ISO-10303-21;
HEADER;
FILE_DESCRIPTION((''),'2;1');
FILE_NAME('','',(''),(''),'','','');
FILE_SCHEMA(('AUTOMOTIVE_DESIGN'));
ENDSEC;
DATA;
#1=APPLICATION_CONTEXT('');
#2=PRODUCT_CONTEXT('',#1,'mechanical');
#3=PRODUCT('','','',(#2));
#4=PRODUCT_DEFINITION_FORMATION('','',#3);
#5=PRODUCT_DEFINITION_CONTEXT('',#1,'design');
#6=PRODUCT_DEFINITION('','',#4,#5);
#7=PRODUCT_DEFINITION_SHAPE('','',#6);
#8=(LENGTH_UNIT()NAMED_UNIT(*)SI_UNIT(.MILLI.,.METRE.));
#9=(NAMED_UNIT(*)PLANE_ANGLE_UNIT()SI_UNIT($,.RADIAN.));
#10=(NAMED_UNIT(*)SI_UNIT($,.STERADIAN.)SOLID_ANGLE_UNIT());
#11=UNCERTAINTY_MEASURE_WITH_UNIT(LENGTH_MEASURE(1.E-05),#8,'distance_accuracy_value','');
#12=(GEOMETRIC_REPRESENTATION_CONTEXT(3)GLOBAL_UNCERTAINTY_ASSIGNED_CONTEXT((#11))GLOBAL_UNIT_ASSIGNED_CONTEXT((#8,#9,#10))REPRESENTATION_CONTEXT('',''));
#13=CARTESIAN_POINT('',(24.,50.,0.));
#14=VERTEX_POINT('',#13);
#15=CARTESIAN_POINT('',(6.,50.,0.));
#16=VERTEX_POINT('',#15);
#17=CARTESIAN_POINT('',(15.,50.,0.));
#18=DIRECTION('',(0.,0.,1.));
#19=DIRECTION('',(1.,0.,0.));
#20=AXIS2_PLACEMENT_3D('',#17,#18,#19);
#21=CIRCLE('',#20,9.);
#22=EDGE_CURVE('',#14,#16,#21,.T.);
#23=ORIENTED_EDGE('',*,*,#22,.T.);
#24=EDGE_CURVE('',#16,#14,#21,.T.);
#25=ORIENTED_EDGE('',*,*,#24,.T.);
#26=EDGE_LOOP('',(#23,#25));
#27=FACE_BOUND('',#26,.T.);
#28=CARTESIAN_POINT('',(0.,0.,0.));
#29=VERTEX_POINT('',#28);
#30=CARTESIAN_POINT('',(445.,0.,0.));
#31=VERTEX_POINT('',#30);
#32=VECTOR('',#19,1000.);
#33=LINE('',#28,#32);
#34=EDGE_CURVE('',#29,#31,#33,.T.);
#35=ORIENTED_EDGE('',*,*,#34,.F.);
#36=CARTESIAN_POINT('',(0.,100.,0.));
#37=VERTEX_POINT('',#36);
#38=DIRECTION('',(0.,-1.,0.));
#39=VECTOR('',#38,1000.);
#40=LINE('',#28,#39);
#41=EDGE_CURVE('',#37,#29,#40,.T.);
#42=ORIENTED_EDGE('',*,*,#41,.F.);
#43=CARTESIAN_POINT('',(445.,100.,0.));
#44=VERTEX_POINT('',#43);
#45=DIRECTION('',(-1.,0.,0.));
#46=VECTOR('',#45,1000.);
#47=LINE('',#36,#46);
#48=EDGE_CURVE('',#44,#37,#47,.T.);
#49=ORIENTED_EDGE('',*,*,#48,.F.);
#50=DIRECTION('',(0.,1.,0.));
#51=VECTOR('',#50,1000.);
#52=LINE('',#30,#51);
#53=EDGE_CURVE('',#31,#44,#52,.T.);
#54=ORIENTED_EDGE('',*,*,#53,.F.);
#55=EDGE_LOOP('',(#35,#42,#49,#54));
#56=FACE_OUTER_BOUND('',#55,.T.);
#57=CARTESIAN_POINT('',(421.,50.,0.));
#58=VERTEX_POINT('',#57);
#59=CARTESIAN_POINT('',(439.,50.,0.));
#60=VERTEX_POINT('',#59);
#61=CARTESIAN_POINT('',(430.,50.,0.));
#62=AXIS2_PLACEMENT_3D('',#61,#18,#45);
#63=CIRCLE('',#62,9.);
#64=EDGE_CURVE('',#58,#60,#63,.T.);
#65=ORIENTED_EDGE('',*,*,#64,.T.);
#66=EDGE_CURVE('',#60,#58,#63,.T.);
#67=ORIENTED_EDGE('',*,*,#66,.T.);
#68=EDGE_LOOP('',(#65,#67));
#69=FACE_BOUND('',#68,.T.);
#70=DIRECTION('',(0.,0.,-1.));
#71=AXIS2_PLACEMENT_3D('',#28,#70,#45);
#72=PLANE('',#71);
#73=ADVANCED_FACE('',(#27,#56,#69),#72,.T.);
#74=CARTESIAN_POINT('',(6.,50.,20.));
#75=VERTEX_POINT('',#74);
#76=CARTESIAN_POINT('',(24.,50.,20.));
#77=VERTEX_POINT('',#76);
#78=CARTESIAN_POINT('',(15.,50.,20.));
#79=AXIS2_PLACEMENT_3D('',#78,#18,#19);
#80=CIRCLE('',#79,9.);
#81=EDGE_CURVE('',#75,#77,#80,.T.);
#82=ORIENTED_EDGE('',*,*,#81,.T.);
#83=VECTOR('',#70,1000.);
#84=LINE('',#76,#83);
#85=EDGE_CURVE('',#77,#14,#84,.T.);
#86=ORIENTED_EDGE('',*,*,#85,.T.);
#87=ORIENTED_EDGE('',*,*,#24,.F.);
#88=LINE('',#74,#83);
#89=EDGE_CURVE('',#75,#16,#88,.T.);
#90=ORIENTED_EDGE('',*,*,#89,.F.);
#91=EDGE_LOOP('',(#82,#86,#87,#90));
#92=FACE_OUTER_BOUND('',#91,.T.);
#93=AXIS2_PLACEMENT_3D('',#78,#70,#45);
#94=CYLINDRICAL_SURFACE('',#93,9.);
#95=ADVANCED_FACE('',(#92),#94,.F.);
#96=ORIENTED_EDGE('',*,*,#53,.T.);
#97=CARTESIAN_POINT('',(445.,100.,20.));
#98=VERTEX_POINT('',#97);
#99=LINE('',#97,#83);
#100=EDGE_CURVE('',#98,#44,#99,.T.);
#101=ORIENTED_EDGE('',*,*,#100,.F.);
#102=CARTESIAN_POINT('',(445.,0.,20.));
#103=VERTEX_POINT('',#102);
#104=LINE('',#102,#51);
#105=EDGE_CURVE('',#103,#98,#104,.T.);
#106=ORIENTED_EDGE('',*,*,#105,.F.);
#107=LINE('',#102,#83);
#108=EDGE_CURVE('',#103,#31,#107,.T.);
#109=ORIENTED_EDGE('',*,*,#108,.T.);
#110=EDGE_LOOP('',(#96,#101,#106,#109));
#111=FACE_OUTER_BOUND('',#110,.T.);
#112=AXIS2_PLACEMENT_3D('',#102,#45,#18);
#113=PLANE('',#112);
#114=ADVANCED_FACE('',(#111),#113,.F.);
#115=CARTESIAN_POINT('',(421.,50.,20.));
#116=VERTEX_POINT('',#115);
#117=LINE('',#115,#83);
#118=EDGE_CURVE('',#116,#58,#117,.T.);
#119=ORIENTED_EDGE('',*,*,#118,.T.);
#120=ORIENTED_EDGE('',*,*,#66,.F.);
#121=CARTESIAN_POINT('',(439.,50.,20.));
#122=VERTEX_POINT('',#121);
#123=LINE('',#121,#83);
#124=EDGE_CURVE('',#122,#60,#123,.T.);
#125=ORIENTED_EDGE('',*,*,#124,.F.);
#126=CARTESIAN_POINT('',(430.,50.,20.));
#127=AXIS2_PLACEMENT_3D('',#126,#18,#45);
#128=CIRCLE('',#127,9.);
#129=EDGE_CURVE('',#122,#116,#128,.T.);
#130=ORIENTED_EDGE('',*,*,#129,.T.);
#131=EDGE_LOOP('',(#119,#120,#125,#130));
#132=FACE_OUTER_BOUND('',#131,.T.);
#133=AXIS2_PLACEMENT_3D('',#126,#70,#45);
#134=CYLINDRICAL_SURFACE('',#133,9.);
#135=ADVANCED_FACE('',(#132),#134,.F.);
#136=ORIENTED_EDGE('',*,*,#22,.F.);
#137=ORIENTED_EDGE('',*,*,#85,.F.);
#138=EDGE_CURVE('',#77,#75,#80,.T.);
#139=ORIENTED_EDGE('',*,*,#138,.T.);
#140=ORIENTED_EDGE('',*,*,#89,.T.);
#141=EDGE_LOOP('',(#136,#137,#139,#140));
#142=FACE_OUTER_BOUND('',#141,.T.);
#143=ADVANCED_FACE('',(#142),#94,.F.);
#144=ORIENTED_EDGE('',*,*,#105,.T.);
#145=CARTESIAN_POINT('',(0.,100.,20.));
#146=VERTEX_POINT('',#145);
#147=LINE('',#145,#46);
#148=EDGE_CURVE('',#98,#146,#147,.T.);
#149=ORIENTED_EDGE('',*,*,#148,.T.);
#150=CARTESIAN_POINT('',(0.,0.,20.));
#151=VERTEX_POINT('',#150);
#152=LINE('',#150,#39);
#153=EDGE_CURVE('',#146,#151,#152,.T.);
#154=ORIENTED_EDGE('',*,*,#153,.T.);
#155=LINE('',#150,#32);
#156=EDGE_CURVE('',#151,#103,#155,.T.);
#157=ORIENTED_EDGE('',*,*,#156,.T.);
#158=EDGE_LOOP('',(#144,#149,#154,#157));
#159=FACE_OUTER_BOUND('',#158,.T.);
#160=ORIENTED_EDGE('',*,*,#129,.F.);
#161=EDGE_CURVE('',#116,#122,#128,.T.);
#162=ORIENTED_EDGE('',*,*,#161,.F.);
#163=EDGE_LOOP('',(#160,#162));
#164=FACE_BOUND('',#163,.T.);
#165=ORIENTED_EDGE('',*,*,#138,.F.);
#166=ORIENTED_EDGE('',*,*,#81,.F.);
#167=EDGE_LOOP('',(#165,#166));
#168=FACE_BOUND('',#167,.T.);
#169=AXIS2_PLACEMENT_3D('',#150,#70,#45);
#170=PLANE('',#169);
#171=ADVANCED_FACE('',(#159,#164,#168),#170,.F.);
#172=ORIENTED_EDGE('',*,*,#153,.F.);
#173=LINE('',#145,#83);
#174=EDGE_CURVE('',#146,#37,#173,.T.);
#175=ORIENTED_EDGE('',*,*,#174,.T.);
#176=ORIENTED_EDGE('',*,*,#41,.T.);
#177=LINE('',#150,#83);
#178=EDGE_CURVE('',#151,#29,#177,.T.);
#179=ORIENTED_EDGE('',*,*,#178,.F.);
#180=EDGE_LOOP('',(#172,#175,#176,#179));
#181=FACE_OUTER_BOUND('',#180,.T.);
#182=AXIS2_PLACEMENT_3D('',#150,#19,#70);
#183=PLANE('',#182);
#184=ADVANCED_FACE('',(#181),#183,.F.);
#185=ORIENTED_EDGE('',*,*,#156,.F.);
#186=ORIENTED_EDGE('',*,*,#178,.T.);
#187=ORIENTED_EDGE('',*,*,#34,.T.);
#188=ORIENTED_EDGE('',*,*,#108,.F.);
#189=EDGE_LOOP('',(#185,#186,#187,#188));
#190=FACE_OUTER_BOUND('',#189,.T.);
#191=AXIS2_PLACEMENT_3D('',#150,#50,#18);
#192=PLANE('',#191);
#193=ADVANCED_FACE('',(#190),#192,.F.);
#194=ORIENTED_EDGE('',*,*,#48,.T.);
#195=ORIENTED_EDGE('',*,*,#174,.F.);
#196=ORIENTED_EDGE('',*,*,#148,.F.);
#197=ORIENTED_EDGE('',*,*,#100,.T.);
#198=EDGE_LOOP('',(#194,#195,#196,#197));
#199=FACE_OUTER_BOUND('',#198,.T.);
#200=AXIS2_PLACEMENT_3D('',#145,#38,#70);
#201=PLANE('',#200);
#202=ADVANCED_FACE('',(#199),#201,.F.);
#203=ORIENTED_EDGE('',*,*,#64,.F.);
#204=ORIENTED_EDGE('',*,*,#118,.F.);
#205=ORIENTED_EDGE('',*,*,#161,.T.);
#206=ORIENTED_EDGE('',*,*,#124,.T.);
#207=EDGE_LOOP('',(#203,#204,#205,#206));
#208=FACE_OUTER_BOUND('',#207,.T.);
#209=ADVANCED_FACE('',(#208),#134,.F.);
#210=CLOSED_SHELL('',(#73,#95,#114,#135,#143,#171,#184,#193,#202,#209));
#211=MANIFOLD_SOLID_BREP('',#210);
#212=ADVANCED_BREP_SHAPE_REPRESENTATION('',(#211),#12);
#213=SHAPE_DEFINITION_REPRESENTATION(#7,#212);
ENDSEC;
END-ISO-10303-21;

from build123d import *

# Parameters (mm, degrees)
SKETCH1_W           = 445
SKETCH1_H           = 100
SKETCH1_R           = 9
BOSS_EXTRUDE1_DEPTH = 20


with BuildPart() as part:
    # Sketch1 → Boss-Extrude1 (new body)
    with BuildSketch(Plane.XY):
        with Locations((222.5, 50)):
            Rectangle(SKETCH1_W, SKETCH1_H)
        with Locations((15, 50)):
            Circle(SKETCH1_R, mode=Mode.SUBTRACT)
        with Locations(Location((430, 50, 0), (0, 0, 180))):
            Circle(SKETCH1_R, mode=Mode.SUBTRACT)
    extrude(amount=BOSS_EXTRUDE1_DEPTH)


solid = part.part
